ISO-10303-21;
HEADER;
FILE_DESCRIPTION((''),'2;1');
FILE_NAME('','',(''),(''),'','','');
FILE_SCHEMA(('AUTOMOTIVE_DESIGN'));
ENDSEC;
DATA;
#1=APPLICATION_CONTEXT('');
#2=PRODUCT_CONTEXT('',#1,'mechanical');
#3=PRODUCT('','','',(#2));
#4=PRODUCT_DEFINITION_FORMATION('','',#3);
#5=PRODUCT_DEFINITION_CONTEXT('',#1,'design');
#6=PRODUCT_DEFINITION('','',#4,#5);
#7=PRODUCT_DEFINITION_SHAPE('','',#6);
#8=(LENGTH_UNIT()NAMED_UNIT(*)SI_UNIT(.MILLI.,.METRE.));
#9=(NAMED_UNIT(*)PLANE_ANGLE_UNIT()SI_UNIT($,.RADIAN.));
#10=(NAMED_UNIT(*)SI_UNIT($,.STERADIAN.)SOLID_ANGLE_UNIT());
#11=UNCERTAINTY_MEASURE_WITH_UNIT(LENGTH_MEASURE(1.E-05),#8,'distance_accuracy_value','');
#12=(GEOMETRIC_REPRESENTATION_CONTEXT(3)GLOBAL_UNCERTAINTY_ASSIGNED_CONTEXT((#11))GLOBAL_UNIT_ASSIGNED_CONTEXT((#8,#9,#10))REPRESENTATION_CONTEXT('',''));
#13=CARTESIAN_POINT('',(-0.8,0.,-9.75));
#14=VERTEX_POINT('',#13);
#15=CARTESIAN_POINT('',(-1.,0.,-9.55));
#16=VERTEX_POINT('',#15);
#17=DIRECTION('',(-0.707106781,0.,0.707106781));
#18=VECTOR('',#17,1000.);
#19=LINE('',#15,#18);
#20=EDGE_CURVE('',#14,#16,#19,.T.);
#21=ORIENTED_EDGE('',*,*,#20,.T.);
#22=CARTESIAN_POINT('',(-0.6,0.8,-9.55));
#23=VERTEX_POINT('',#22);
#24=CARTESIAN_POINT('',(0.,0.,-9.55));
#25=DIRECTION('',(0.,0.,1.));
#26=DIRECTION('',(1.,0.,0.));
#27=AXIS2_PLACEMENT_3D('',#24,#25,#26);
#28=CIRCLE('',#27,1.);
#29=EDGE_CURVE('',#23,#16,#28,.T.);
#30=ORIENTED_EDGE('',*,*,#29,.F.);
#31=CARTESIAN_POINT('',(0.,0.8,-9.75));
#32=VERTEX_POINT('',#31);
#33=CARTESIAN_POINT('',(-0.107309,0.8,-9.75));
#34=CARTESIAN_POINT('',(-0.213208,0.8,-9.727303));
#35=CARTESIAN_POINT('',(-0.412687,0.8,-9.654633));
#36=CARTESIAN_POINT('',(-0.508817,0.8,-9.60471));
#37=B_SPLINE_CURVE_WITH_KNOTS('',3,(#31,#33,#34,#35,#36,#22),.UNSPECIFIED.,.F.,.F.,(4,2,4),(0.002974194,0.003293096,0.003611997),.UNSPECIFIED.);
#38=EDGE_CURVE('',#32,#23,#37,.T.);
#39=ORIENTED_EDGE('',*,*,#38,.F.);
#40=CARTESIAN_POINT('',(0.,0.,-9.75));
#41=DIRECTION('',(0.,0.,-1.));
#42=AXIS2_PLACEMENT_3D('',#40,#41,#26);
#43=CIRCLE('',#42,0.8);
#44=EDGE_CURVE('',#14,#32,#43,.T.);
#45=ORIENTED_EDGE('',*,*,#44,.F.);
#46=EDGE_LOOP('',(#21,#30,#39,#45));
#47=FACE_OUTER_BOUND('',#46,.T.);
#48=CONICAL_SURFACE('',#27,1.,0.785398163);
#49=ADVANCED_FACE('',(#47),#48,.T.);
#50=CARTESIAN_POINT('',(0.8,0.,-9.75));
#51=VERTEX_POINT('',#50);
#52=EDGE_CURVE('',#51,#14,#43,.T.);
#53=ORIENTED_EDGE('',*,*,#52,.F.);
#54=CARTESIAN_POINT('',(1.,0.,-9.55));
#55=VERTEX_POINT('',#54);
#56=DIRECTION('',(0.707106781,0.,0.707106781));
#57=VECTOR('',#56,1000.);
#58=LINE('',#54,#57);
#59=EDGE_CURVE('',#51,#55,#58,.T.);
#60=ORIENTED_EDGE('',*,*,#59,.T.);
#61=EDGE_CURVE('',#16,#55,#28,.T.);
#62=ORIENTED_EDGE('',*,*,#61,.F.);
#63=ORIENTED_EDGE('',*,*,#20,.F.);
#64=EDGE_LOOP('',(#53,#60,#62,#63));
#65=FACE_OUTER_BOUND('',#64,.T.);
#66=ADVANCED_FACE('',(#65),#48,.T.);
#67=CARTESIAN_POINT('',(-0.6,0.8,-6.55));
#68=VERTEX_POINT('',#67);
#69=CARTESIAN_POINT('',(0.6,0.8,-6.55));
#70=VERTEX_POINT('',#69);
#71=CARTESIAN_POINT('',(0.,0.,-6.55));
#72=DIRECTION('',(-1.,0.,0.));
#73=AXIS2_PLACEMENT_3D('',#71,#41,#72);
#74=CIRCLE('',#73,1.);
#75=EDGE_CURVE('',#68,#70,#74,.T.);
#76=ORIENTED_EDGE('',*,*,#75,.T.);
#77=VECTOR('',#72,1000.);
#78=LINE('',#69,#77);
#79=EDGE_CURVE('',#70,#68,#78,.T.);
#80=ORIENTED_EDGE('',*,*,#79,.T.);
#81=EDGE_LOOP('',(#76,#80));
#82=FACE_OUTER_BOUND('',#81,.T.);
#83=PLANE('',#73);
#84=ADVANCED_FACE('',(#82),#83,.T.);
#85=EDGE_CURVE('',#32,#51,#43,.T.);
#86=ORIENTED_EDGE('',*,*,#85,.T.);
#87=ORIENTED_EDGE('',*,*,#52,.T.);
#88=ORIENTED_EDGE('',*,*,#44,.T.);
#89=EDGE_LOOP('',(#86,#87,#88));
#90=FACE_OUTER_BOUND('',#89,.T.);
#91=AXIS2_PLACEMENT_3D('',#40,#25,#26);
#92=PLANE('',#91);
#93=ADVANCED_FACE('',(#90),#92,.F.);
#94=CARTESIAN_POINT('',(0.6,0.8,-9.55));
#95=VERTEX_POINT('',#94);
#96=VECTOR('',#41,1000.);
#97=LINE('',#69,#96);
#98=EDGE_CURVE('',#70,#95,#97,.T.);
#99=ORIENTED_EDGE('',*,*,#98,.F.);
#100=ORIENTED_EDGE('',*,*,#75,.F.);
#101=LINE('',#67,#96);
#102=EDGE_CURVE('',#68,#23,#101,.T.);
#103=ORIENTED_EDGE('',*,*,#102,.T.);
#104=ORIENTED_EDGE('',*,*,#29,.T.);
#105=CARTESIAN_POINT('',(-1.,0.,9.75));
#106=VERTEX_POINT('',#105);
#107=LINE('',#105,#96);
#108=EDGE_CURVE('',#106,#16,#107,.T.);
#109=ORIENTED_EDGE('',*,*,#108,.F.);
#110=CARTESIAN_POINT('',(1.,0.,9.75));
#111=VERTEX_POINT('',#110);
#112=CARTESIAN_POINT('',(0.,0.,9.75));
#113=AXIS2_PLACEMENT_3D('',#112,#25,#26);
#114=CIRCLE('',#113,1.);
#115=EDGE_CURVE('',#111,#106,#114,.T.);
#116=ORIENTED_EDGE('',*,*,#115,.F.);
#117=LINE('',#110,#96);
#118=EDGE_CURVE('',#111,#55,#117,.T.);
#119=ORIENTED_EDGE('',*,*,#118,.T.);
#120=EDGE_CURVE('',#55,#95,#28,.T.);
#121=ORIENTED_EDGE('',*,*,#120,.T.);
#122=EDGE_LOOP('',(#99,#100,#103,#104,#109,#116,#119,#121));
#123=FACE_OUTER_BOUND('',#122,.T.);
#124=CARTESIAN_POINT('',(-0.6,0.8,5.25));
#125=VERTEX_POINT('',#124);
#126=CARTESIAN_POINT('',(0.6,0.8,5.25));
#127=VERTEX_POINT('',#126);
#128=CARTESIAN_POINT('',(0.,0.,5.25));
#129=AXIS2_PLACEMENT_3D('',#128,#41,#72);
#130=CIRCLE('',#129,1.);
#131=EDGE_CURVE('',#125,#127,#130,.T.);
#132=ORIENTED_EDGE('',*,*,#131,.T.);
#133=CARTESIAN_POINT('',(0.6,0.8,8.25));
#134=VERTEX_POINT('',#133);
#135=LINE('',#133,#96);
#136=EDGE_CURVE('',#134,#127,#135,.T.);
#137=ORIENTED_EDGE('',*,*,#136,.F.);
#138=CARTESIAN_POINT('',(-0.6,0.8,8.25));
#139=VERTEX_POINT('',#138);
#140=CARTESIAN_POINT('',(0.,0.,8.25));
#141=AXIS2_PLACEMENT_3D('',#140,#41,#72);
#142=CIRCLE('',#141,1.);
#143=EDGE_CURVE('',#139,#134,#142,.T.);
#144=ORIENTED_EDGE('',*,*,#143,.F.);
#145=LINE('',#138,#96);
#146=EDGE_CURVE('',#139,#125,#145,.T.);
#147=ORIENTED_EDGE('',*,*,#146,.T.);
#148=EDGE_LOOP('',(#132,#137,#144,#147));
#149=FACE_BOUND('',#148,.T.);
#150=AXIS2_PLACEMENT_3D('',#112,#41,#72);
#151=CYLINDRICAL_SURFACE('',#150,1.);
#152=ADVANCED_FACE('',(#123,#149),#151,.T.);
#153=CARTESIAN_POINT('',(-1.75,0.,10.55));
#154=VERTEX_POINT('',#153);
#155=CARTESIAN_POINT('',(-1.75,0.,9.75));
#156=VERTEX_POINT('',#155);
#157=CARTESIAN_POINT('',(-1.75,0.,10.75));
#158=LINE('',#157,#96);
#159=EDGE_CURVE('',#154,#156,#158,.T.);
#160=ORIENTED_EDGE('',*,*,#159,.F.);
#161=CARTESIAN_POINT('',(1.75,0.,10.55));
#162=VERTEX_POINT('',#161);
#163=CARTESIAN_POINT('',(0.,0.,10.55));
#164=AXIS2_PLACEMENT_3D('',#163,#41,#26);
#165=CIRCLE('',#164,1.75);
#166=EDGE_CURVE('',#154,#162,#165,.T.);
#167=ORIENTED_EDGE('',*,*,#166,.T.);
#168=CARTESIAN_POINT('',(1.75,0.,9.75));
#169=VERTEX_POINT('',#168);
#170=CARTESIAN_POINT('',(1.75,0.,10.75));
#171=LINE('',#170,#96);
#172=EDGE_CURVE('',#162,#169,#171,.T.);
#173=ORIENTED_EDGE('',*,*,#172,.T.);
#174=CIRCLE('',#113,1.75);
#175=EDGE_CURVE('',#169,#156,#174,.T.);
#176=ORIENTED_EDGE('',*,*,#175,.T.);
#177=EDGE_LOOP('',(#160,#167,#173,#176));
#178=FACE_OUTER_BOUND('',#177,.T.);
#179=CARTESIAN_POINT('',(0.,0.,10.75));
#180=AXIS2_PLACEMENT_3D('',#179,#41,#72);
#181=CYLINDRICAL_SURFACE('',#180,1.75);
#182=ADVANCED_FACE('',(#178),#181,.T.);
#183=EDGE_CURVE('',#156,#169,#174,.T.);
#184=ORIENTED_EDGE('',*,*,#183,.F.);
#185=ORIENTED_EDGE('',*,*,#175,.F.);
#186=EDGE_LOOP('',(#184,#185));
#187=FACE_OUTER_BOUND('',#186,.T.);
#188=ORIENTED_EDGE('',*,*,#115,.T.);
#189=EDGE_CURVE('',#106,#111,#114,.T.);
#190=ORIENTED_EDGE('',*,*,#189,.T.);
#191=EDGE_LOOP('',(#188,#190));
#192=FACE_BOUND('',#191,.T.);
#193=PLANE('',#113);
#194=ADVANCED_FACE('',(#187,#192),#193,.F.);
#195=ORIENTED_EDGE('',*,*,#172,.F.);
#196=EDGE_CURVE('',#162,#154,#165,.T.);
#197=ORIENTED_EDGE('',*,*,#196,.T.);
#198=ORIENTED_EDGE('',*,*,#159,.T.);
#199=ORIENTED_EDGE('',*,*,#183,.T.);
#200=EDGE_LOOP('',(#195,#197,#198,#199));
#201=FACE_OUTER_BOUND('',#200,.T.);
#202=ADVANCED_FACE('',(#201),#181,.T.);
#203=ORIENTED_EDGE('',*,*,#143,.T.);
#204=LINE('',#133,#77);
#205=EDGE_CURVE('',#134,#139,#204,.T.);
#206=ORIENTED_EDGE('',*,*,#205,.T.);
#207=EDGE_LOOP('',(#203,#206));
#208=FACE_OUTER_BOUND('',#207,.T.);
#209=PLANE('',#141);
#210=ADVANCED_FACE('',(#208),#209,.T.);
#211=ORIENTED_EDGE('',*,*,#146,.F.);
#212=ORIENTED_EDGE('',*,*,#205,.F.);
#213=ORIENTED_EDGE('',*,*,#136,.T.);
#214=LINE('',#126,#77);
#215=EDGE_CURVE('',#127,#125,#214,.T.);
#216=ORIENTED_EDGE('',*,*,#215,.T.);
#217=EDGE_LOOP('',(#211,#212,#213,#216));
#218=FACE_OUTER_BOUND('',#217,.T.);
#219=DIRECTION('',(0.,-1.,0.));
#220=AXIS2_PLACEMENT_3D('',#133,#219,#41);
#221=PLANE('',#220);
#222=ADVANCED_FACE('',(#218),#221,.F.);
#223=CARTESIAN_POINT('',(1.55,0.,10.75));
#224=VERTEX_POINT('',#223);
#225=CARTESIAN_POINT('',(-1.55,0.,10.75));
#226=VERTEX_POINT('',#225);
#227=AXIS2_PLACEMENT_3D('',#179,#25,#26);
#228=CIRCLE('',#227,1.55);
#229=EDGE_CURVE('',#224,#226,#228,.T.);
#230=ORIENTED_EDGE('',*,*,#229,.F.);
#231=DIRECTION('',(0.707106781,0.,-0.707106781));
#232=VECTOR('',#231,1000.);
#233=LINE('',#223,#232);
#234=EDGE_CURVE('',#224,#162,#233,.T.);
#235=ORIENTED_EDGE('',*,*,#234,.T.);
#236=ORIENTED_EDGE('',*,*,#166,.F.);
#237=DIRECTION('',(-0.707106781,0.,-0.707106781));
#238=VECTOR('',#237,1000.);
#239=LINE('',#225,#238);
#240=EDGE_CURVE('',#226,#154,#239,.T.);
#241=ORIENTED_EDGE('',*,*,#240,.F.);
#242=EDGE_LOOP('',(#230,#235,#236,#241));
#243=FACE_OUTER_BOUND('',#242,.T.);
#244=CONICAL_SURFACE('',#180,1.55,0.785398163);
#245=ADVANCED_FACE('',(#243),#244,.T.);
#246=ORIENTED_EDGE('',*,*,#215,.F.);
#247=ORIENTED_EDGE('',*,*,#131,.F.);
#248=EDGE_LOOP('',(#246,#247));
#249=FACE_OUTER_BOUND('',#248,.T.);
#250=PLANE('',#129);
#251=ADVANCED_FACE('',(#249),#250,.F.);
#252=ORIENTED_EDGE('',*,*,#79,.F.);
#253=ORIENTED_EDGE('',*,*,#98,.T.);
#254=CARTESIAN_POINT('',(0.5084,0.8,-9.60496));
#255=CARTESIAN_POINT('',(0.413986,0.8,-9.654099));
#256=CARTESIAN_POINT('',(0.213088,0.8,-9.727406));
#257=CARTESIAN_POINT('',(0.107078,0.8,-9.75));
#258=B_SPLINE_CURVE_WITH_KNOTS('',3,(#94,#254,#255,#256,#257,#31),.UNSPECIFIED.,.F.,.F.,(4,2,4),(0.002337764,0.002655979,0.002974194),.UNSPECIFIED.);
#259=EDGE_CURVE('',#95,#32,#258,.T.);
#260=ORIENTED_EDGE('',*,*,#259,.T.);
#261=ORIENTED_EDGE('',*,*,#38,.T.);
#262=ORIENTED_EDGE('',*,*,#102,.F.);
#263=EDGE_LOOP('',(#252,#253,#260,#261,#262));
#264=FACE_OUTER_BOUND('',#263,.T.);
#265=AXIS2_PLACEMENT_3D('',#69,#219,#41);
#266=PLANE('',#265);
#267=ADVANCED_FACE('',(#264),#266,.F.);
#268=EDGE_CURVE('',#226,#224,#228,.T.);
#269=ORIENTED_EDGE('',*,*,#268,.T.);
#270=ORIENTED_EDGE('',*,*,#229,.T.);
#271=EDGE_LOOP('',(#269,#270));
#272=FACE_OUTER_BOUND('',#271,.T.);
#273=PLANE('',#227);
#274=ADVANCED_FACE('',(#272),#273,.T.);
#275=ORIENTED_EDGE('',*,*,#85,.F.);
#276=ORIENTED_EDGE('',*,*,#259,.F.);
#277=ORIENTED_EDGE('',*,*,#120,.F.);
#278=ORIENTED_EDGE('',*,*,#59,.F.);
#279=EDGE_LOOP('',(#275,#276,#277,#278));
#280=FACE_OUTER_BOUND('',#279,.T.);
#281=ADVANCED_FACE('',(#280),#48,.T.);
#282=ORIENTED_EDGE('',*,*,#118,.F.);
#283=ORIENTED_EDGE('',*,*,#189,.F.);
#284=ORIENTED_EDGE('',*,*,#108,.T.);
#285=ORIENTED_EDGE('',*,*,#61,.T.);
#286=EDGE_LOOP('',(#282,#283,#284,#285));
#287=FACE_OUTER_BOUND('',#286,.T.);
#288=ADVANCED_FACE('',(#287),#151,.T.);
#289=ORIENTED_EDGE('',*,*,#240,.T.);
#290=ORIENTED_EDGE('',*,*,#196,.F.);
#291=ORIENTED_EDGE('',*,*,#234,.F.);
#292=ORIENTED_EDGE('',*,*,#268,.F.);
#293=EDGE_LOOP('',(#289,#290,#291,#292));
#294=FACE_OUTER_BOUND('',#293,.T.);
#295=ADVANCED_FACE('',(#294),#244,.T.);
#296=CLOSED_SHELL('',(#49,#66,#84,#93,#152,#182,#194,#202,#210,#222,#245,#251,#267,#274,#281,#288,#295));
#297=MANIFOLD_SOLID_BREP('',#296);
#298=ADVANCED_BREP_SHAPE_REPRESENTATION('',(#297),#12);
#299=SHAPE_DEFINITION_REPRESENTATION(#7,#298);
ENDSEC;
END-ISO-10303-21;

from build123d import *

# Parameters (mm, degrees)
SKETCH1_R           = 1
BOSS_EXTRUDE1_DEPTH = 9.75
SKETCH2_R           = 1.75
BOSS_EXTRUDE2_DEPTH = 1
CHAMFER1_SIZE       = 0.2
CUT_EXTRUDE1_START  = -3.2
CUT_EXTRUDE1_DEPTH  = 3.2
CUT_EXTRUDE2_DEPTH  = 1.5


with BuildPart() as part:
    # Sketch1 → Boss-Extrude1 (new, symmetric)
    with BuildSketch(Plane.XY):
        Circle(SKETCH1_R)
    extrude(amount=BOSS_EXTRUDE1_DEPTH, both=True)

    # Sketch2 → Boss-Extrude2 (add)
    with BuildSketch(Plane.XY.offset(9.75)):
        Circle(SKETCH2_R)
    extrude(amount=BOSS_EXTRUDE2_DEPTH)

    # Chamfer1
    chamfer1_edges = [part.edges().sort_by_distance(p)[0] for p in [
        (-1, 0, -9.75),
        (-1.75, 0, 10.75),
    ]]
    chamfer(chamfer1_edges, length=CHAMFER1_SIZE)

    # Sketch3 → Cut-Extrude1 (cut)
    with BuildSketch(Plane(origin=(0, 0, -9.75), x_dir=(-1, 0, 0), z_dir=(0, 0, -1)).offset(CUT_EXTRUDE1_START)):
        with BuildLine():
            Line((-0.6, 0.8), (0.6, 0.8))
            ThreePointArc((0.6, 0.8), (0, 1), (-0.6, 0.8))
        make_face()
    extrude(amount=CUT_EXTRUDE1_DEPTH, mode=Mode.SUBTRACT)

    # Sketch4 → Cut-Extrude2 (cut, symmetric)
    with BuildSketch(Plane(origin=(0, 0, 6.75), x_dir=(-1, 0, 0), z_dir=(0, 0, -1))):
        with BuildLine():
            Line((-0.6, 0.8), (0.6, 0.8))
            ThreePointArc((0.6, 0.8), (0, 1), (-0.6, 0.8))
        make_face()
    extrude(amount=CUT_EXTRUDE2_DEPTH, both=True, mode=Mode.SUBTRACT)


solid = part.part
